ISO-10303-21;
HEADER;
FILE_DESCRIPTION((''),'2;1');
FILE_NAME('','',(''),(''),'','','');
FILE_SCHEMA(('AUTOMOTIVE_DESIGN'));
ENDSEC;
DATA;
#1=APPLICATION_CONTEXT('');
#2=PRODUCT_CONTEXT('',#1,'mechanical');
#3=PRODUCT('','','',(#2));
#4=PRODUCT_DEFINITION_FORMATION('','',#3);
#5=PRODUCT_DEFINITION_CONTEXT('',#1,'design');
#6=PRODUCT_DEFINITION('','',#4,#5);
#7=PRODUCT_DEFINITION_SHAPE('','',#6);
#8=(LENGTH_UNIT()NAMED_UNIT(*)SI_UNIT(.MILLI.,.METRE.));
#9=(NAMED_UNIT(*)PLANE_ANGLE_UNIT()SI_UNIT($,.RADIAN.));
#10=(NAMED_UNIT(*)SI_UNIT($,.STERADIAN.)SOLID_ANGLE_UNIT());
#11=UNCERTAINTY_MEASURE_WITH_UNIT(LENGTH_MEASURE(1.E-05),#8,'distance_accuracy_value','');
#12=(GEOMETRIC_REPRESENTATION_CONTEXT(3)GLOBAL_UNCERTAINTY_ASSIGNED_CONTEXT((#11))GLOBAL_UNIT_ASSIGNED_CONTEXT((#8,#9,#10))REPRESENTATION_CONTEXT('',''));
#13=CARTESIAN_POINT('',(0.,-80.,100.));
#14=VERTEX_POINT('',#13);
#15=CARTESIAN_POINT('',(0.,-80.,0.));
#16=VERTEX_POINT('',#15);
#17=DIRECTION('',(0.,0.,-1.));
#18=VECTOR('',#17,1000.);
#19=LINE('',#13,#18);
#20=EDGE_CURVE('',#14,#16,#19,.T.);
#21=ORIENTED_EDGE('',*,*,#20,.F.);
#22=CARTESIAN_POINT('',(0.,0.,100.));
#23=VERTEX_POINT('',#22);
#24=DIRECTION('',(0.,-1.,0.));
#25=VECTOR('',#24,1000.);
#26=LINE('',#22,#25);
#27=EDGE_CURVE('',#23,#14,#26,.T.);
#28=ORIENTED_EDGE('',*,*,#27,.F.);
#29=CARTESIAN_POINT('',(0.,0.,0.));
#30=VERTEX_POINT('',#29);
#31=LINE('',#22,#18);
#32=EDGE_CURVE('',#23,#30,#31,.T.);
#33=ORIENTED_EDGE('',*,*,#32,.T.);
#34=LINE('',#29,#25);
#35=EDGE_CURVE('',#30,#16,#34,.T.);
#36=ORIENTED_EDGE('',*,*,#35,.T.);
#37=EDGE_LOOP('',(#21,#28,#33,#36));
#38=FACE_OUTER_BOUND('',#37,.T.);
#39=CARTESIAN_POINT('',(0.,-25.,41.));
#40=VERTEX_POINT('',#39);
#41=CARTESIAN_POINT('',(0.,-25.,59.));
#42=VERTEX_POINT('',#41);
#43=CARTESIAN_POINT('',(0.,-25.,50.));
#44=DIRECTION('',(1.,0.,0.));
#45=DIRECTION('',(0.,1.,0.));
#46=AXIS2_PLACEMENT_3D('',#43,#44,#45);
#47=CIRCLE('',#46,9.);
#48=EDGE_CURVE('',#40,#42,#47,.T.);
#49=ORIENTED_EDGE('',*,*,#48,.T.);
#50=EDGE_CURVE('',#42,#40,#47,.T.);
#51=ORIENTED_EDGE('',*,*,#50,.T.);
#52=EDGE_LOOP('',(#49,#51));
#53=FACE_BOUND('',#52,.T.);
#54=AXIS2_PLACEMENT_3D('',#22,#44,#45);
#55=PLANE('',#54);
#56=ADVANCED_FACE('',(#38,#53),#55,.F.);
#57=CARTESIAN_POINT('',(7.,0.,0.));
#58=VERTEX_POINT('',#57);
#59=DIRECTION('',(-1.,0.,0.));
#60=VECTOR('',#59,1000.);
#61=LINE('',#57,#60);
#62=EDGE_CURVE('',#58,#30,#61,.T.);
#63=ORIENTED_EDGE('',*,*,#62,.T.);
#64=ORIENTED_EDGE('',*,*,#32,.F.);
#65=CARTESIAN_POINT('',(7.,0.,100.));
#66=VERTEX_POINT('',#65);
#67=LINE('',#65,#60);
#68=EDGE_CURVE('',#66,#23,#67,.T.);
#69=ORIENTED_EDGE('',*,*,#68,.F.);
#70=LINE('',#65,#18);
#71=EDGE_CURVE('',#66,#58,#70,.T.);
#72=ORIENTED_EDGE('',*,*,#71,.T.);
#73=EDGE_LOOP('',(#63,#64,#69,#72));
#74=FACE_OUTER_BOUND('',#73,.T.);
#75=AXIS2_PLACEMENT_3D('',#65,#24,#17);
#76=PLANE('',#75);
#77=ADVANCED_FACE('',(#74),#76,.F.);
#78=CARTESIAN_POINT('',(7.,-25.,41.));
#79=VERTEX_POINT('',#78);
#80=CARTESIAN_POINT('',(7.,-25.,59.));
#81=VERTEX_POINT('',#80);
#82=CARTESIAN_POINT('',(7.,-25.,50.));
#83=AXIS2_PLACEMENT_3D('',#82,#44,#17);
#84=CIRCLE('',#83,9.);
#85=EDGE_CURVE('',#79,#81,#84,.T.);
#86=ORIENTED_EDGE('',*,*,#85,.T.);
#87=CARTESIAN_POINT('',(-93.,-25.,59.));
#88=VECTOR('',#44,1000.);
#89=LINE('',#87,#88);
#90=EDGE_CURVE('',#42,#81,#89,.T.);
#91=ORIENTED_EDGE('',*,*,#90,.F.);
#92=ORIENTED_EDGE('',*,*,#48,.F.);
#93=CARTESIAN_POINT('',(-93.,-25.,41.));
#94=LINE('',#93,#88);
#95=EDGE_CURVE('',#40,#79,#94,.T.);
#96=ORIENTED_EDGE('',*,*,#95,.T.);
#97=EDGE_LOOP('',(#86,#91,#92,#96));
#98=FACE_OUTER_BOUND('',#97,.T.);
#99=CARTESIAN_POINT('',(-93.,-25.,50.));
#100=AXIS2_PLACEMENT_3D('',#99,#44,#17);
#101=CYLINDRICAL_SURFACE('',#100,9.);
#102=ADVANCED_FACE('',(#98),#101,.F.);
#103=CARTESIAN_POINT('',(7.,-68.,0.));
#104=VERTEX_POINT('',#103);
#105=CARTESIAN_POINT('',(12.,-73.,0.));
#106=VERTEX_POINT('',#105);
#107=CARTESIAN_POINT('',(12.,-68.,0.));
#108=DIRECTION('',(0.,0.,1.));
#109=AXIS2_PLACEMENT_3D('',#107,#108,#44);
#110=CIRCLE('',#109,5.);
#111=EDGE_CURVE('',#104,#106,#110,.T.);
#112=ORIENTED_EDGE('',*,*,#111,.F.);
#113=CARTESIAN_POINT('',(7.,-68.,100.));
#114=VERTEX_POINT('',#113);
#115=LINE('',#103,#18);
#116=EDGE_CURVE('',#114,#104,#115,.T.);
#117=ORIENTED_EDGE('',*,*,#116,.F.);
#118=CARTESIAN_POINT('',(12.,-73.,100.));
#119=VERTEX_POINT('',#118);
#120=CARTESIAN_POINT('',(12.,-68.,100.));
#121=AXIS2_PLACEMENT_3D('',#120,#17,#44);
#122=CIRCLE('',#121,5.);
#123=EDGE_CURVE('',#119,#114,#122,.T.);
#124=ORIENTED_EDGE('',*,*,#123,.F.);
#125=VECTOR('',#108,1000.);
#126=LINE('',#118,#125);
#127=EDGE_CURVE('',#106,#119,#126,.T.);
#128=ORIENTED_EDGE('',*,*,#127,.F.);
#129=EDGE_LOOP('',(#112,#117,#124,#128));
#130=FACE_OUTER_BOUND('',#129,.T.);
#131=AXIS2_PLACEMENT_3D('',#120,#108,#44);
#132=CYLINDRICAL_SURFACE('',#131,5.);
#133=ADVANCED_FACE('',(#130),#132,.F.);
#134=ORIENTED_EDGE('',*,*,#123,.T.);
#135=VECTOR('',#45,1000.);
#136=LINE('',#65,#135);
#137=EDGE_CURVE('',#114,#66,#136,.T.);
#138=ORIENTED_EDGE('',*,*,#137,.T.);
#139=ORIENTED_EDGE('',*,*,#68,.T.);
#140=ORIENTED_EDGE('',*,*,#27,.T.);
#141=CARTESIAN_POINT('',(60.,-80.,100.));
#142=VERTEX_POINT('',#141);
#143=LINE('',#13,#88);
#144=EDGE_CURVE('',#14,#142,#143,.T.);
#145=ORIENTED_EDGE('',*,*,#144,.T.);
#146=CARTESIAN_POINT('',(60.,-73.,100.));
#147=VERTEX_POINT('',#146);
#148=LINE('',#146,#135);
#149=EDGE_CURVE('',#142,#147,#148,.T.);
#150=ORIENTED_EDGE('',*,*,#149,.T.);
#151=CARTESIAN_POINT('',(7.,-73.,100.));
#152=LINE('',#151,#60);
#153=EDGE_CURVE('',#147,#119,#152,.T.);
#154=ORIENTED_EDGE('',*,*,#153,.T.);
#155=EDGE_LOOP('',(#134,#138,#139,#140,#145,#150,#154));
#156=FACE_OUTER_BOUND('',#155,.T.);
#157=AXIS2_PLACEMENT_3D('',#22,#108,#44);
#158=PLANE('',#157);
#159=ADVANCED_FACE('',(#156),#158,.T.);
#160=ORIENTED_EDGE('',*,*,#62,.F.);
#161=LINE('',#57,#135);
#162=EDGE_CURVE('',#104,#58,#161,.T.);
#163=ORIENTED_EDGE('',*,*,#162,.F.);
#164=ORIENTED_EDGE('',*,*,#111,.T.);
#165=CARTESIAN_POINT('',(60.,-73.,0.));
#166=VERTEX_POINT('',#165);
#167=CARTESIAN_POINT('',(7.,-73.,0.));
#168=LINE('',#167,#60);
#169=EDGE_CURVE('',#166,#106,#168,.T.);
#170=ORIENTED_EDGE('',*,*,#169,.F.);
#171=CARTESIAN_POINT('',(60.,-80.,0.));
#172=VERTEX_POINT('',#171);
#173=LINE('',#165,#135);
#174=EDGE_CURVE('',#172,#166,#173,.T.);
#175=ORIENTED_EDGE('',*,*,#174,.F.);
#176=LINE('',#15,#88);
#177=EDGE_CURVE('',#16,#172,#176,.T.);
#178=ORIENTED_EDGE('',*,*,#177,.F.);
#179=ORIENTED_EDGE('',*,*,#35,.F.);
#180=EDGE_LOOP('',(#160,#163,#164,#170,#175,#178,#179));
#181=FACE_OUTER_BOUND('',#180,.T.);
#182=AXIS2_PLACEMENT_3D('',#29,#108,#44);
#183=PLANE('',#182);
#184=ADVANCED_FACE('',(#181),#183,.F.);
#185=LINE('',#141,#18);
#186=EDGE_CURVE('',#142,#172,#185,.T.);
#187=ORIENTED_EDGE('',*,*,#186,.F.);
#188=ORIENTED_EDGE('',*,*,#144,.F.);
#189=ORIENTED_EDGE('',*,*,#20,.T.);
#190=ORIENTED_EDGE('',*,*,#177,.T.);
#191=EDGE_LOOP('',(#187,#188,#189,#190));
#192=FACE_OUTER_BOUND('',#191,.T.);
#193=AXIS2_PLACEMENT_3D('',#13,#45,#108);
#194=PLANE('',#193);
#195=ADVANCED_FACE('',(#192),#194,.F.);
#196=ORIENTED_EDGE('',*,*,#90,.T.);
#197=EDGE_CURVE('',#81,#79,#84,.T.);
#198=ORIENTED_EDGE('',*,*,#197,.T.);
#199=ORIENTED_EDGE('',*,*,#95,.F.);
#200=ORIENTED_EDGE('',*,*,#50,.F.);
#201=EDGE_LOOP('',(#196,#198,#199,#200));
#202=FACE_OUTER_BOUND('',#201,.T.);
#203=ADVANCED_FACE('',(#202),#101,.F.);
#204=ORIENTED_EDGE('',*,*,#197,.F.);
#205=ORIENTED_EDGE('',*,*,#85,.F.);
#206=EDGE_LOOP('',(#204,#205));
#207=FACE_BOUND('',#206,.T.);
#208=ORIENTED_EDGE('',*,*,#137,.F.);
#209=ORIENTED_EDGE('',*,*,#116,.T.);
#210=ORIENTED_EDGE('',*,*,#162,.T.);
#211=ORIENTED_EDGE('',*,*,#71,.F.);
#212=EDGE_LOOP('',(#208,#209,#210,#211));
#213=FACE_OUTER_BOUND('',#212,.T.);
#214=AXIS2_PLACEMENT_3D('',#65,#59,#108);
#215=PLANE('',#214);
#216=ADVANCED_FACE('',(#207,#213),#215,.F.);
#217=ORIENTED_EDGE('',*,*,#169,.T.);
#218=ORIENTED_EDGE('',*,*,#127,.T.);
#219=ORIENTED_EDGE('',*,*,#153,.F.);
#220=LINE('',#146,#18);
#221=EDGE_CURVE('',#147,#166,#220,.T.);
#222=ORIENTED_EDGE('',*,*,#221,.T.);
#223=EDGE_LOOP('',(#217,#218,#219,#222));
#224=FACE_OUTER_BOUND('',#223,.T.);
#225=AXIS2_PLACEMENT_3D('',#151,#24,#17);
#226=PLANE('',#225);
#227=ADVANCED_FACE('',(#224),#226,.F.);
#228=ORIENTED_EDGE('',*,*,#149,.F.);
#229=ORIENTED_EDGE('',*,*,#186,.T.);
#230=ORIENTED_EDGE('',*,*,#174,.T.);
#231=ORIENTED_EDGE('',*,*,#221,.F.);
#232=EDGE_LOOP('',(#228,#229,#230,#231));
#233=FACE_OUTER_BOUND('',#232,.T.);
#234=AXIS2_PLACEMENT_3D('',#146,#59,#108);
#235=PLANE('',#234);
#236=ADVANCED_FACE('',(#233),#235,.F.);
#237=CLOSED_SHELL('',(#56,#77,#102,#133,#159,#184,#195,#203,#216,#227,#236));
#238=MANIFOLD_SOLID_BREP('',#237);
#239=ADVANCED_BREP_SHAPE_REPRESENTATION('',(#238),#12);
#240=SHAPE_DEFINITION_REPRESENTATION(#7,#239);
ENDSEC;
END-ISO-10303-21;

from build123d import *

# Parameters (mm, degrees)
BOSS_EXTRUDE1_DEPTH = 100
SKETCH2_R           = 9
CUT_EXTRUDE1_DEPTH  = 100
FILLET1_R           = 5


with BuildPart() as part:
    # Sketch1 → Boss-Extrude1 (new body)
    with BuildSketch(Plane.XY):
        Polygon((0, 0), (0, -80), (60, -80), (60, -73), (7, -73), (7, 0), align=None)
    extrude(amount=BOSS_EXTRUDE1_DEPTH)

    # Sketch2 → Cut-Extrude1 (cut)
    with BuildSketch(Plane(origin=(7, 0, 0), x_dir=(0, 0, -1), z_dir=(1, 0, 0))):
        with Locations((-50, -25)):
            Circle(SKETCH2_R)
    extrude(amount=-CUT_EXTRUDE1_DEPTH, mode=Mode.SUBTRACT)

    # Fillet1
    fillet1_edges = [part.edges().sort_by_distance(p)[0] for p in [
        (7, -73, 50),
    ]]
    fillet(fillet1_edges, radius=FILLET1_R)


solid = part.part
